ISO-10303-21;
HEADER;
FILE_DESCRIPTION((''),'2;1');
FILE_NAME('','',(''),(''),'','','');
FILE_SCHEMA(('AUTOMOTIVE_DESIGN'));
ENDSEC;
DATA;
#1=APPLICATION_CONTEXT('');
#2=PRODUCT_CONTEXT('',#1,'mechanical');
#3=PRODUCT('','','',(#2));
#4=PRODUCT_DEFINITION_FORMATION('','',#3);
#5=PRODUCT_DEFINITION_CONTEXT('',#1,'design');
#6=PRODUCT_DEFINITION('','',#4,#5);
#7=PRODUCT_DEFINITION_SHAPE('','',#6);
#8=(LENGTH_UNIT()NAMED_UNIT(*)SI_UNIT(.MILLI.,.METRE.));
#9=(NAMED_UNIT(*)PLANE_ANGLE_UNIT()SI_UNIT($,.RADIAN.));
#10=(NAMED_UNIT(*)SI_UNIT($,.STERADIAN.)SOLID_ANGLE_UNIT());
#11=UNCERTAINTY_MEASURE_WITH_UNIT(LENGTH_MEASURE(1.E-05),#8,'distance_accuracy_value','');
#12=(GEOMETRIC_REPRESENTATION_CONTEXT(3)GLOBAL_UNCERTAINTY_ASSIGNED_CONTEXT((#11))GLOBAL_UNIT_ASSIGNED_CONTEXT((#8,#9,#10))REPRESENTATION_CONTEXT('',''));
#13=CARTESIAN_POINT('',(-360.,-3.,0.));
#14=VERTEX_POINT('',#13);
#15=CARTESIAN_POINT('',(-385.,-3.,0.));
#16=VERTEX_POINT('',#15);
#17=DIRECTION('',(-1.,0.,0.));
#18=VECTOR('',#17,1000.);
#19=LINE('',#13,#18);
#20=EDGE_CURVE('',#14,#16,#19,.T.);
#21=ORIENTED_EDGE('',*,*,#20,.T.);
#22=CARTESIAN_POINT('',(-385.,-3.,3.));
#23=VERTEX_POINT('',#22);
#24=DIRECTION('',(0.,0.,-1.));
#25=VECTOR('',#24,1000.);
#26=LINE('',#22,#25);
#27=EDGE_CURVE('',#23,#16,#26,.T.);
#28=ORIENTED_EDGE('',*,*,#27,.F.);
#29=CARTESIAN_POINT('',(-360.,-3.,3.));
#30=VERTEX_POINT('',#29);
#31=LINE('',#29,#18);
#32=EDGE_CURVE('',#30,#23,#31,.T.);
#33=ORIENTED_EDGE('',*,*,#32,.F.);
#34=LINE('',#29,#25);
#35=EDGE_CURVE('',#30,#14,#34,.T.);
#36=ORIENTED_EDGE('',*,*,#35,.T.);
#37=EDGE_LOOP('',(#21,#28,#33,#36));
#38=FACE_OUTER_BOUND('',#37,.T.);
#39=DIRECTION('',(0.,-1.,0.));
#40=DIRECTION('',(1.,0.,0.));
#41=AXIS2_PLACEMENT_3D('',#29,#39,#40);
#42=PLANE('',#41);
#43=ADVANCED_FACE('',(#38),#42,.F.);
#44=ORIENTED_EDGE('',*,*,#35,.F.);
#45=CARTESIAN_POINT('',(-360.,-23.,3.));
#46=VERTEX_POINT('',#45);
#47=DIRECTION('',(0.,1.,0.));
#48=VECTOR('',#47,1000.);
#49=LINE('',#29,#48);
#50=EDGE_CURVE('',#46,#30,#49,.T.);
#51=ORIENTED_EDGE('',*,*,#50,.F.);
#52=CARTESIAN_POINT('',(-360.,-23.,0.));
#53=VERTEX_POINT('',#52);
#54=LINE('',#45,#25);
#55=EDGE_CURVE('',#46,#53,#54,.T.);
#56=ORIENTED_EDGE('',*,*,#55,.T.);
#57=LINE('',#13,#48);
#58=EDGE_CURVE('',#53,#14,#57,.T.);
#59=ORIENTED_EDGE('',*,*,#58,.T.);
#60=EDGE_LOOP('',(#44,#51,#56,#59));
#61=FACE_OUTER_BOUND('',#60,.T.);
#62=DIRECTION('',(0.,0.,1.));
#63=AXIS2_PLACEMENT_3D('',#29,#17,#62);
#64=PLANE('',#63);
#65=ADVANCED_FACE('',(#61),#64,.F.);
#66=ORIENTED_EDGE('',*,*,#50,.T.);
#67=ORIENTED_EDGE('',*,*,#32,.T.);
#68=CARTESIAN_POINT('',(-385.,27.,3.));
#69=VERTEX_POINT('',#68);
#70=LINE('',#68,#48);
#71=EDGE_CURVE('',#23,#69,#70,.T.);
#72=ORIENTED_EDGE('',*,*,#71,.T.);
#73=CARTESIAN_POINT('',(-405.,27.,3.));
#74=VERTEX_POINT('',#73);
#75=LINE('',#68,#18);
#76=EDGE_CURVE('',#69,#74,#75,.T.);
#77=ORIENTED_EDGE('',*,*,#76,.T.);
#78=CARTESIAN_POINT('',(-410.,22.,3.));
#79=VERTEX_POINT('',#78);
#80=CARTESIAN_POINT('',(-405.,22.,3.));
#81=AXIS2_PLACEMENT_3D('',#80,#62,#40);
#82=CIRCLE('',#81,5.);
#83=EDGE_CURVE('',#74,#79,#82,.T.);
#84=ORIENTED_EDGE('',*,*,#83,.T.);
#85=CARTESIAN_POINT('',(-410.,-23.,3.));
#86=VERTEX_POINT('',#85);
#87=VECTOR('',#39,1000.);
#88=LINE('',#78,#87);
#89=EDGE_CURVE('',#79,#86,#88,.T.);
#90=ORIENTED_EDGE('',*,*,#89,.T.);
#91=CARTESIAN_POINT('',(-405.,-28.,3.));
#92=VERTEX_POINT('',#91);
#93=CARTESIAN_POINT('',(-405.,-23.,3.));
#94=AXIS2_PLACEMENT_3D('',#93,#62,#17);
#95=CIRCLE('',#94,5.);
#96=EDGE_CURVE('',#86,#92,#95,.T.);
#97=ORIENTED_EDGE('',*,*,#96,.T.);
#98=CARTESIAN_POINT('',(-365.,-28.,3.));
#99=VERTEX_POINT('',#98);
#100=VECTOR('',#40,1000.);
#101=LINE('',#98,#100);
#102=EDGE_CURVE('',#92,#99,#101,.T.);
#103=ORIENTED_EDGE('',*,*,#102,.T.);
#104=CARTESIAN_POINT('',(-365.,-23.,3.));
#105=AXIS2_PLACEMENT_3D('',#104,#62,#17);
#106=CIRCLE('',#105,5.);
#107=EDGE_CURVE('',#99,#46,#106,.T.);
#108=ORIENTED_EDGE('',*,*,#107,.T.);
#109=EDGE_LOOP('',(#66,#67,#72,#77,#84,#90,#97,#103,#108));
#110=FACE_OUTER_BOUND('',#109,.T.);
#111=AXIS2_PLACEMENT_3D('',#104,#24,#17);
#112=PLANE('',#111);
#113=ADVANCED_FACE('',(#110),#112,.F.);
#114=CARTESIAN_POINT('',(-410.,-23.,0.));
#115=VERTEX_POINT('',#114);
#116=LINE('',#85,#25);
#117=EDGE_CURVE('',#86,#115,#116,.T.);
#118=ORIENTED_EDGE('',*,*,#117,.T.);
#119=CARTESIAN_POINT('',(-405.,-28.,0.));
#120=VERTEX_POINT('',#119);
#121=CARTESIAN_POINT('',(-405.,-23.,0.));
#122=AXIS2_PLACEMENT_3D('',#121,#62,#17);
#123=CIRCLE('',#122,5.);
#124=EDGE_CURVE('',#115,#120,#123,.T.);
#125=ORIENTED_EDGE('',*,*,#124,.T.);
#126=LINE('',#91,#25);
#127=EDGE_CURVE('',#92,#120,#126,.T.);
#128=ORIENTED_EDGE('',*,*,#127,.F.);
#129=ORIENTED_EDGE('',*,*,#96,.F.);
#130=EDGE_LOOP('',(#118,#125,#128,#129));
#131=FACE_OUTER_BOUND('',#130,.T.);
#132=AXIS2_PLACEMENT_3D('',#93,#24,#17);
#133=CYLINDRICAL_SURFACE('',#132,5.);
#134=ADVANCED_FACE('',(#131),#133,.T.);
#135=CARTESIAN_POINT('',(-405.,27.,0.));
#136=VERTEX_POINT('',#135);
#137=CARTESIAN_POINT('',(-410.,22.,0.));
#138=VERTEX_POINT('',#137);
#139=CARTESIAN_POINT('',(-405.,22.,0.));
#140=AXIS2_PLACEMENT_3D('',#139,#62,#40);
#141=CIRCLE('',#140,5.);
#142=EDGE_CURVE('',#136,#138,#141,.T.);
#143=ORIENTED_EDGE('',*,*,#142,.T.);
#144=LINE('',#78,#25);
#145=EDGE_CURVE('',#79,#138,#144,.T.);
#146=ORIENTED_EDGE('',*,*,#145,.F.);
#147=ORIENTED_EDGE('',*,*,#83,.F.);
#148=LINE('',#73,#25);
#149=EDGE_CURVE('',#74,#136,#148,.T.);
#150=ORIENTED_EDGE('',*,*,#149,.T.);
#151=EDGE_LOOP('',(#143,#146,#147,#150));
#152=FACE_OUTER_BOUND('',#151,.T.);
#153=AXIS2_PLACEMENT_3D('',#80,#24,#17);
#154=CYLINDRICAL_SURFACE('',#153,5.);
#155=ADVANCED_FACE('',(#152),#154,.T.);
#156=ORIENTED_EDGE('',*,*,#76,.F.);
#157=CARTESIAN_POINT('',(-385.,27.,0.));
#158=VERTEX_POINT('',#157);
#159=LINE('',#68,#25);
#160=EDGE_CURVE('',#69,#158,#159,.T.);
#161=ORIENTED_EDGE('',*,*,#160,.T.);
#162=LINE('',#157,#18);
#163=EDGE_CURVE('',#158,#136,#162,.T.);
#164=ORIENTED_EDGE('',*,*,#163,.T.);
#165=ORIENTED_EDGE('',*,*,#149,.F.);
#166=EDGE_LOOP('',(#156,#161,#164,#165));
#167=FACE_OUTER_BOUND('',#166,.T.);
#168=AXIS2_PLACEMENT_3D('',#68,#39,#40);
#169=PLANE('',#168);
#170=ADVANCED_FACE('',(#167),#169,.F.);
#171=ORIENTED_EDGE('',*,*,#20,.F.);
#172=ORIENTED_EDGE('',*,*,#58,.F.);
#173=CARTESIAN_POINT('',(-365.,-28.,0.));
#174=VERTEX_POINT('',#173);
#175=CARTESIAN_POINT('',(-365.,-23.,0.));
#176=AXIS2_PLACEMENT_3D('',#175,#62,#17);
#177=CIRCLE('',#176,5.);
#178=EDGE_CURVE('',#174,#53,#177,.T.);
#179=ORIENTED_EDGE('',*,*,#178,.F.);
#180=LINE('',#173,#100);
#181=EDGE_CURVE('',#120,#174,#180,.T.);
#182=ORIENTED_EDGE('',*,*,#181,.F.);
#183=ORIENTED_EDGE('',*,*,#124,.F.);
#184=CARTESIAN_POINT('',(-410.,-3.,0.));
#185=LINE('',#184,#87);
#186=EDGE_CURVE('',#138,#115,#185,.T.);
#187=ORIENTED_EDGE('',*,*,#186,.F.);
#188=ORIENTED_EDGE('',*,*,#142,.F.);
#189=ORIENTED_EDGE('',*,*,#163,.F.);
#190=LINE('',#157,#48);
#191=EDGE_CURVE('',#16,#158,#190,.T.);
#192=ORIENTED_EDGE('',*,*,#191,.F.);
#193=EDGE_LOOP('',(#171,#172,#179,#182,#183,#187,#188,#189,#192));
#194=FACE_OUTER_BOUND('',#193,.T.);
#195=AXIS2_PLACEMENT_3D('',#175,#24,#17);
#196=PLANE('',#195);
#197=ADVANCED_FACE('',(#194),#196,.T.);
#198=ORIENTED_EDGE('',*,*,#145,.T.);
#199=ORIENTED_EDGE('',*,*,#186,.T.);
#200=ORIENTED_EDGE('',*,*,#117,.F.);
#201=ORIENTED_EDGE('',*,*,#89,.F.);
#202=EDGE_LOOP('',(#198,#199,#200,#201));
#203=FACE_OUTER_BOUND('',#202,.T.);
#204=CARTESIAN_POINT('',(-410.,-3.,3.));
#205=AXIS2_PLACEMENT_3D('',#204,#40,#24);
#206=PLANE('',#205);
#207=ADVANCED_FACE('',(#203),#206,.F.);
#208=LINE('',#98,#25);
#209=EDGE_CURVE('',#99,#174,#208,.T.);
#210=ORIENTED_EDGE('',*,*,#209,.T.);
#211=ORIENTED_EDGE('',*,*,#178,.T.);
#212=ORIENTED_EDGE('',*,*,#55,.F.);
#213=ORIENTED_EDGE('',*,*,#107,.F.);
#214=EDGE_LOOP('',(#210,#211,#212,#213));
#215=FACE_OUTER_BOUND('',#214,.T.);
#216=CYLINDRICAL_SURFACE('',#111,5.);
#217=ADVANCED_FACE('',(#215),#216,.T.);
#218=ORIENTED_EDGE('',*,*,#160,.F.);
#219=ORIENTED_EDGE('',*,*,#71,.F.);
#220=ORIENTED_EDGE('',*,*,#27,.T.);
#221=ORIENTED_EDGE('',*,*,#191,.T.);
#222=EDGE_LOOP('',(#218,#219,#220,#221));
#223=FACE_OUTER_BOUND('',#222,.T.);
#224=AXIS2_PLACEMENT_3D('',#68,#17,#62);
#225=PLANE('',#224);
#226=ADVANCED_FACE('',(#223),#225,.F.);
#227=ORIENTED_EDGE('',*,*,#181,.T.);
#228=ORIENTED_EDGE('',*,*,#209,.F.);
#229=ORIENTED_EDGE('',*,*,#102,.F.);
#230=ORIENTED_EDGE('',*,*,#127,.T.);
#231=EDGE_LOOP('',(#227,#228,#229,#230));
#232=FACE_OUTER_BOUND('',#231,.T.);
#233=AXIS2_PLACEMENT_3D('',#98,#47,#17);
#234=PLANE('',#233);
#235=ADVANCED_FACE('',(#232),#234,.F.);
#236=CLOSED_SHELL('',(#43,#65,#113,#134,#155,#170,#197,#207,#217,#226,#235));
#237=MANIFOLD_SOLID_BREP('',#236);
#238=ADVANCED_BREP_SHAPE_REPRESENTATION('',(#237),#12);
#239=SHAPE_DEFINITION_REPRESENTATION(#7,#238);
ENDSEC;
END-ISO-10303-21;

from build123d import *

# Parameters (mm, degrees)
BOSS_EXTRUDE1_DEPTH = 3


with BuildPart() as part:
    # Sketch1 → Boss-Extrude1 (new body)
    with BuildSketch(Plane.XY):
        with BuildLine():
            Line((-360, -3), (-385, -3))
            Line((-385, -3), (-385, 27))
            Line((-385, 27), (-405, 27))
            ThreePointArc((-405, 27), (-408.535533906, 25.535533906), (-410, 22))
            Line((-410, 22), (-410, -3))
            Line((-410, -3), (-410, -23))
            ThreePointArc((-410, -23), (-408.535533906, -26.535533906), (-405, -28))
            Line((-405, -28), (-365, -28))
            ThreePointArc((-365, -28), (-361.464466094, -26.535533906), (-360, -23))
            Line((-360, -23), (-360, -3))
        make_face()
    extrude(amount=BOSS_EXTRUDE1_DEPTH)


solid = part.part
